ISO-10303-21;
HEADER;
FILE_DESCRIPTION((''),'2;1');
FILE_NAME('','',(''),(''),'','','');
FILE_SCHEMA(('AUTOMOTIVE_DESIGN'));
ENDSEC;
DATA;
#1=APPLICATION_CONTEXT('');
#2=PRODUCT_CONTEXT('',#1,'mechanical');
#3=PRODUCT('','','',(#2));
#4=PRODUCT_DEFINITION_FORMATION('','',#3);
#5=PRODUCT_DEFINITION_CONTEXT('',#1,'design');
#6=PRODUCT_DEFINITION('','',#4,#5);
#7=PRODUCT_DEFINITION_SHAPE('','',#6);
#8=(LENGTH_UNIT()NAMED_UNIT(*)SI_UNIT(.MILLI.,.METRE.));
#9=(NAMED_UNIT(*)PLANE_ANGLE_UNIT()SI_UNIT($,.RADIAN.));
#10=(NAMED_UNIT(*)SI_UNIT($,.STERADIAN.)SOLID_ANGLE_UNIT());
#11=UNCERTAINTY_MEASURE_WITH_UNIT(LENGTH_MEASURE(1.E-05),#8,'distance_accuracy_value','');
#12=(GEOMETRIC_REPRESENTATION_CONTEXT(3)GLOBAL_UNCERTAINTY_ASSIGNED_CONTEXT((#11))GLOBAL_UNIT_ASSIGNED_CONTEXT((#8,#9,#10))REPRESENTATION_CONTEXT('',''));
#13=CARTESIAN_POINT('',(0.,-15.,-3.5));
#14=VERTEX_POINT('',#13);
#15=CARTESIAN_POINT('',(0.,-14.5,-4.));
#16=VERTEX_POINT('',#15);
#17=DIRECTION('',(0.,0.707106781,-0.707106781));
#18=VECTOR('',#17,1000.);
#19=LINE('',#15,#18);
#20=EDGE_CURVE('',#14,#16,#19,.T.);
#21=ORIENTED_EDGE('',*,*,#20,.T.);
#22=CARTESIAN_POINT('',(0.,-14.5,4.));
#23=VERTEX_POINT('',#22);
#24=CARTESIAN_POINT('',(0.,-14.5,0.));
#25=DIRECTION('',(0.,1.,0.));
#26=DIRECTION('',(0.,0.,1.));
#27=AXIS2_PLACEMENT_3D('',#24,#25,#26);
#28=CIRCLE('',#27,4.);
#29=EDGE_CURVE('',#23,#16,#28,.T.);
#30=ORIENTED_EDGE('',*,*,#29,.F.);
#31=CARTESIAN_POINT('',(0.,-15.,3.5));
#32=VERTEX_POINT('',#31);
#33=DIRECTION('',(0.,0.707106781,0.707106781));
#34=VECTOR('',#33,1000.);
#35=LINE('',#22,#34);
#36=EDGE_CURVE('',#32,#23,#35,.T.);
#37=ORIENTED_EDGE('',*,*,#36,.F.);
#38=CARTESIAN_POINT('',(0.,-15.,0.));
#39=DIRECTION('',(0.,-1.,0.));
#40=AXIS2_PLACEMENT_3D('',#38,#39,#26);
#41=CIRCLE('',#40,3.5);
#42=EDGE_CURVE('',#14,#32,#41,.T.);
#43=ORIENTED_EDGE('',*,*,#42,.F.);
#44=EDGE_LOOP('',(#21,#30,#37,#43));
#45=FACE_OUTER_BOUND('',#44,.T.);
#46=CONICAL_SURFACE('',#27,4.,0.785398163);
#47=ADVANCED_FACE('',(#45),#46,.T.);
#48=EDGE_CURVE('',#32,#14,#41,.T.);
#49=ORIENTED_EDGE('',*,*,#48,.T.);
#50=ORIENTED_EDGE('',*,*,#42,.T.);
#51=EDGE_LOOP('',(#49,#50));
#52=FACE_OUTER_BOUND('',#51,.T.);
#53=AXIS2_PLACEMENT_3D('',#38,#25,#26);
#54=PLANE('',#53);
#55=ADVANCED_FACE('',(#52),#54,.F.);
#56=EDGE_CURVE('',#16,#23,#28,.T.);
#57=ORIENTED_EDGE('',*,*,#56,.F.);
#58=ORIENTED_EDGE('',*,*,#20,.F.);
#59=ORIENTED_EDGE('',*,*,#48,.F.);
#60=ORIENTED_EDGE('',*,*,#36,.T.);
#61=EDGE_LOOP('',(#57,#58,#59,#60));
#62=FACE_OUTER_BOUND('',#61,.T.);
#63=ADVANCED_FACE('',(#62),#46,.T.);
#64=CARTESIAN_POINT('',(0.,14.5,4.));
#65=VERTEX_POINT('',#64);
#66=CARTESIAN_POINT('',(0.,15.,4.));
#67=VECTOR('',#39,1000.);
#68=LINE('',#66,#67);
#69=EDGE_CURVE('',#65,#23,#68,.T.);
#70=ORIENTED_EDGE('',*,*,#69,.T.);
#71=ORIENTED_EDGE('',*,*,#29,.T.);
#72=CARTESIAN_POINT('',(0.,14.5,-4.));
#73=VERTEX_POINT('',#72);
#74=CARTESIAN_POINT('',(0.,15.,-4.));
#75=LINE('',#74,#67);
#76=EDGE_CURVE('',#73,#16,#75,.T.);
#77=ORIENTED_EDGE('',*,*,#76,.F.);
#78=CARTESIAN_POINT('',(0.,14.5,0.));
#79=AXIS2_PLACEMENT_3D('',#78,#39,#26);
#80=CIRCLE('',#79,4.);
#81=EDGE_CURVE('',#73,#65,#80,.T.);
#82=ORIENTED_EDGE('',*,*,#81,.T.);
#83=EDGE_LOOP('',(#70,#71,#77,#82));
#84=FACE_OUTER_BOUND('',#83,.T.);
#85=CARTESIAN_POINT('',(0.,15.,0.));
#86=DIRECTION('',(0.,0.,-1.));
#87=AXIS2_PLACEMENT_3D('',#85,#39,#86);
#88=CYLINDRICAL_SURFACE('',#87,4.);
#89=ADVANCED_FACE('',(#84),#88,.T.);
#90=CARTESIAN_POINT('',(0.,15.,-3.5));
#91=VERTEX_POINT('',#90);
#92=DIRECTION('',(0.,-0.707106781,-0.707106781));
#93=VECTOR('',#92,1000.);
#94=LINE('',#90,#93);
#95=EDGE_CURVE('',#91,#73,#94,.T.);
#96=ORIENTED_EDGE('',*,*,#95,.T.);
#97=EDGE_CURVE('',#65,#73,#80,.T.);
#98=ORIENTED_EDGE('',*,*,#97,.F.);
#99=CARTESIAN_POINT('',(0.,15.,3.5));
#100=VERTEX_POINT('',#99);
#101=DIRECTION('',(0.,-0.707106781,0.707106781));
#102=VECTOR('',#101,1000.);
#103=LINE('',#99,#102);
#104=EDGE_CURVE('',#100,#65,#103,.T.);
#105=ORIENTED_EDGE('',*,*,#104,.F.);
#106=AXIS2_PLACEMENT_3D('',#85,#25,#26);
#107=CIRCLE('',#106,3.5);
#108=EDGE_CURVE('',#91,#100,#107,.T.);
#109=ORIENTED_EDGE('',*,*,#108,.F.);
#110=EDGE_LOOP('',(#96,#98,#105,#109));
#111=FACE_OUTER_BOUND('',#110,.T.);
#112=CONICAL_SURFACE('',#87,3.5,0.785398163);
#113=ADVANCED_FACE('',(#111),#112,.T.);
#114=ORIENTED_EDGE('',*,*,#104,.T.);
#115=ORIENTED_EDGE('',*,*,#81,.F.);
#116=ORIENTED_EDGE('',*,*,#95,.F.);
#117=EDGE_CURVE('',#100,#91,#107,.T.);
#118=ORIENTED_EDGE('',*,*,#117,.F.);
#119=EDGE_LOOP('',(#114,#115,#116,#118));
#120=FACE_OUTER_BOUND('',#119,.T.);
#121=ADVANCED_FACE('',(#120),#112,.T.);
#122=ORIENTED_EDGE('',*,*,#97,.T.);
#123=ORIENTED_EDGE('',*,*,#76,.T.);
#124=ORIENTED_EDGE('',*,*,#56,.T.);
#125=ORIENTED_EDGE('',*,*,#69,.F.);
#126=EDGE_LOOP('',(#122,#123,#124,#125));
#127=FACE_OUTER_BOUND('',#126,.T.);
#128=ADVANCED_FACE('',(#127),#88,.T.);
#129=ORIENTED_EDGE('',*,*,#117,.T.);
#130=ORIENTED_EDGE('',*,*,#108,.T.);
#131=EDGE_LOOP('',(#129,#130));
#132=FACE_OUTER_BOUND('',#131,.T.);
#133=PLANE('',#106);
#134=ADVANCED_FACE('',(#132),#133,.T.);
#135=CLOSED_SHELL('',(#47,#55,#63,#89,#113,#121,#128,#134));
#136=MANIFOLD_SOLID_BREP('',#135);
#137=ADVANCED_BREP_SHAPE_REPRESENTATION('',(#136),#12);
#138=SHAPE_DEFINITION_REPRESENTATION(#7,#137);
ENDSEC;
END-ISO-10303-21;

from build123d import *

# Parameters (mm, degrees)
SKETCH1_R           = 4
BOSS_EXTRUDE1_DEPTH = 15
CHAMFER1_SIZE       = 0.5


with BuildPart() as part:
    # Sketch1 → Boss-Extrude1 (new, symmetric)
    with BuildSketch(Plane(origin=(0, 0, 0), x_dir=(1, 0, 0), z_dir=(0, 1, 0))):
        with Locations(Location((0, 0, 0), (0, 0, 270))):
            Circle(SKETCH1_R)
    extrude(amount=BOSS_EXTRUDE1_DEPTH, both=True)

    # Chamfer1
    chamfer1_edges = [part.edges().sort_by_distance(p)[0] for p in [
        (0, -15, -4),
        (0, 15, -4),
    ]]
    chamfer(chamfer1_edges, length=CHAMFER1_SIZE)


solid = part.part
